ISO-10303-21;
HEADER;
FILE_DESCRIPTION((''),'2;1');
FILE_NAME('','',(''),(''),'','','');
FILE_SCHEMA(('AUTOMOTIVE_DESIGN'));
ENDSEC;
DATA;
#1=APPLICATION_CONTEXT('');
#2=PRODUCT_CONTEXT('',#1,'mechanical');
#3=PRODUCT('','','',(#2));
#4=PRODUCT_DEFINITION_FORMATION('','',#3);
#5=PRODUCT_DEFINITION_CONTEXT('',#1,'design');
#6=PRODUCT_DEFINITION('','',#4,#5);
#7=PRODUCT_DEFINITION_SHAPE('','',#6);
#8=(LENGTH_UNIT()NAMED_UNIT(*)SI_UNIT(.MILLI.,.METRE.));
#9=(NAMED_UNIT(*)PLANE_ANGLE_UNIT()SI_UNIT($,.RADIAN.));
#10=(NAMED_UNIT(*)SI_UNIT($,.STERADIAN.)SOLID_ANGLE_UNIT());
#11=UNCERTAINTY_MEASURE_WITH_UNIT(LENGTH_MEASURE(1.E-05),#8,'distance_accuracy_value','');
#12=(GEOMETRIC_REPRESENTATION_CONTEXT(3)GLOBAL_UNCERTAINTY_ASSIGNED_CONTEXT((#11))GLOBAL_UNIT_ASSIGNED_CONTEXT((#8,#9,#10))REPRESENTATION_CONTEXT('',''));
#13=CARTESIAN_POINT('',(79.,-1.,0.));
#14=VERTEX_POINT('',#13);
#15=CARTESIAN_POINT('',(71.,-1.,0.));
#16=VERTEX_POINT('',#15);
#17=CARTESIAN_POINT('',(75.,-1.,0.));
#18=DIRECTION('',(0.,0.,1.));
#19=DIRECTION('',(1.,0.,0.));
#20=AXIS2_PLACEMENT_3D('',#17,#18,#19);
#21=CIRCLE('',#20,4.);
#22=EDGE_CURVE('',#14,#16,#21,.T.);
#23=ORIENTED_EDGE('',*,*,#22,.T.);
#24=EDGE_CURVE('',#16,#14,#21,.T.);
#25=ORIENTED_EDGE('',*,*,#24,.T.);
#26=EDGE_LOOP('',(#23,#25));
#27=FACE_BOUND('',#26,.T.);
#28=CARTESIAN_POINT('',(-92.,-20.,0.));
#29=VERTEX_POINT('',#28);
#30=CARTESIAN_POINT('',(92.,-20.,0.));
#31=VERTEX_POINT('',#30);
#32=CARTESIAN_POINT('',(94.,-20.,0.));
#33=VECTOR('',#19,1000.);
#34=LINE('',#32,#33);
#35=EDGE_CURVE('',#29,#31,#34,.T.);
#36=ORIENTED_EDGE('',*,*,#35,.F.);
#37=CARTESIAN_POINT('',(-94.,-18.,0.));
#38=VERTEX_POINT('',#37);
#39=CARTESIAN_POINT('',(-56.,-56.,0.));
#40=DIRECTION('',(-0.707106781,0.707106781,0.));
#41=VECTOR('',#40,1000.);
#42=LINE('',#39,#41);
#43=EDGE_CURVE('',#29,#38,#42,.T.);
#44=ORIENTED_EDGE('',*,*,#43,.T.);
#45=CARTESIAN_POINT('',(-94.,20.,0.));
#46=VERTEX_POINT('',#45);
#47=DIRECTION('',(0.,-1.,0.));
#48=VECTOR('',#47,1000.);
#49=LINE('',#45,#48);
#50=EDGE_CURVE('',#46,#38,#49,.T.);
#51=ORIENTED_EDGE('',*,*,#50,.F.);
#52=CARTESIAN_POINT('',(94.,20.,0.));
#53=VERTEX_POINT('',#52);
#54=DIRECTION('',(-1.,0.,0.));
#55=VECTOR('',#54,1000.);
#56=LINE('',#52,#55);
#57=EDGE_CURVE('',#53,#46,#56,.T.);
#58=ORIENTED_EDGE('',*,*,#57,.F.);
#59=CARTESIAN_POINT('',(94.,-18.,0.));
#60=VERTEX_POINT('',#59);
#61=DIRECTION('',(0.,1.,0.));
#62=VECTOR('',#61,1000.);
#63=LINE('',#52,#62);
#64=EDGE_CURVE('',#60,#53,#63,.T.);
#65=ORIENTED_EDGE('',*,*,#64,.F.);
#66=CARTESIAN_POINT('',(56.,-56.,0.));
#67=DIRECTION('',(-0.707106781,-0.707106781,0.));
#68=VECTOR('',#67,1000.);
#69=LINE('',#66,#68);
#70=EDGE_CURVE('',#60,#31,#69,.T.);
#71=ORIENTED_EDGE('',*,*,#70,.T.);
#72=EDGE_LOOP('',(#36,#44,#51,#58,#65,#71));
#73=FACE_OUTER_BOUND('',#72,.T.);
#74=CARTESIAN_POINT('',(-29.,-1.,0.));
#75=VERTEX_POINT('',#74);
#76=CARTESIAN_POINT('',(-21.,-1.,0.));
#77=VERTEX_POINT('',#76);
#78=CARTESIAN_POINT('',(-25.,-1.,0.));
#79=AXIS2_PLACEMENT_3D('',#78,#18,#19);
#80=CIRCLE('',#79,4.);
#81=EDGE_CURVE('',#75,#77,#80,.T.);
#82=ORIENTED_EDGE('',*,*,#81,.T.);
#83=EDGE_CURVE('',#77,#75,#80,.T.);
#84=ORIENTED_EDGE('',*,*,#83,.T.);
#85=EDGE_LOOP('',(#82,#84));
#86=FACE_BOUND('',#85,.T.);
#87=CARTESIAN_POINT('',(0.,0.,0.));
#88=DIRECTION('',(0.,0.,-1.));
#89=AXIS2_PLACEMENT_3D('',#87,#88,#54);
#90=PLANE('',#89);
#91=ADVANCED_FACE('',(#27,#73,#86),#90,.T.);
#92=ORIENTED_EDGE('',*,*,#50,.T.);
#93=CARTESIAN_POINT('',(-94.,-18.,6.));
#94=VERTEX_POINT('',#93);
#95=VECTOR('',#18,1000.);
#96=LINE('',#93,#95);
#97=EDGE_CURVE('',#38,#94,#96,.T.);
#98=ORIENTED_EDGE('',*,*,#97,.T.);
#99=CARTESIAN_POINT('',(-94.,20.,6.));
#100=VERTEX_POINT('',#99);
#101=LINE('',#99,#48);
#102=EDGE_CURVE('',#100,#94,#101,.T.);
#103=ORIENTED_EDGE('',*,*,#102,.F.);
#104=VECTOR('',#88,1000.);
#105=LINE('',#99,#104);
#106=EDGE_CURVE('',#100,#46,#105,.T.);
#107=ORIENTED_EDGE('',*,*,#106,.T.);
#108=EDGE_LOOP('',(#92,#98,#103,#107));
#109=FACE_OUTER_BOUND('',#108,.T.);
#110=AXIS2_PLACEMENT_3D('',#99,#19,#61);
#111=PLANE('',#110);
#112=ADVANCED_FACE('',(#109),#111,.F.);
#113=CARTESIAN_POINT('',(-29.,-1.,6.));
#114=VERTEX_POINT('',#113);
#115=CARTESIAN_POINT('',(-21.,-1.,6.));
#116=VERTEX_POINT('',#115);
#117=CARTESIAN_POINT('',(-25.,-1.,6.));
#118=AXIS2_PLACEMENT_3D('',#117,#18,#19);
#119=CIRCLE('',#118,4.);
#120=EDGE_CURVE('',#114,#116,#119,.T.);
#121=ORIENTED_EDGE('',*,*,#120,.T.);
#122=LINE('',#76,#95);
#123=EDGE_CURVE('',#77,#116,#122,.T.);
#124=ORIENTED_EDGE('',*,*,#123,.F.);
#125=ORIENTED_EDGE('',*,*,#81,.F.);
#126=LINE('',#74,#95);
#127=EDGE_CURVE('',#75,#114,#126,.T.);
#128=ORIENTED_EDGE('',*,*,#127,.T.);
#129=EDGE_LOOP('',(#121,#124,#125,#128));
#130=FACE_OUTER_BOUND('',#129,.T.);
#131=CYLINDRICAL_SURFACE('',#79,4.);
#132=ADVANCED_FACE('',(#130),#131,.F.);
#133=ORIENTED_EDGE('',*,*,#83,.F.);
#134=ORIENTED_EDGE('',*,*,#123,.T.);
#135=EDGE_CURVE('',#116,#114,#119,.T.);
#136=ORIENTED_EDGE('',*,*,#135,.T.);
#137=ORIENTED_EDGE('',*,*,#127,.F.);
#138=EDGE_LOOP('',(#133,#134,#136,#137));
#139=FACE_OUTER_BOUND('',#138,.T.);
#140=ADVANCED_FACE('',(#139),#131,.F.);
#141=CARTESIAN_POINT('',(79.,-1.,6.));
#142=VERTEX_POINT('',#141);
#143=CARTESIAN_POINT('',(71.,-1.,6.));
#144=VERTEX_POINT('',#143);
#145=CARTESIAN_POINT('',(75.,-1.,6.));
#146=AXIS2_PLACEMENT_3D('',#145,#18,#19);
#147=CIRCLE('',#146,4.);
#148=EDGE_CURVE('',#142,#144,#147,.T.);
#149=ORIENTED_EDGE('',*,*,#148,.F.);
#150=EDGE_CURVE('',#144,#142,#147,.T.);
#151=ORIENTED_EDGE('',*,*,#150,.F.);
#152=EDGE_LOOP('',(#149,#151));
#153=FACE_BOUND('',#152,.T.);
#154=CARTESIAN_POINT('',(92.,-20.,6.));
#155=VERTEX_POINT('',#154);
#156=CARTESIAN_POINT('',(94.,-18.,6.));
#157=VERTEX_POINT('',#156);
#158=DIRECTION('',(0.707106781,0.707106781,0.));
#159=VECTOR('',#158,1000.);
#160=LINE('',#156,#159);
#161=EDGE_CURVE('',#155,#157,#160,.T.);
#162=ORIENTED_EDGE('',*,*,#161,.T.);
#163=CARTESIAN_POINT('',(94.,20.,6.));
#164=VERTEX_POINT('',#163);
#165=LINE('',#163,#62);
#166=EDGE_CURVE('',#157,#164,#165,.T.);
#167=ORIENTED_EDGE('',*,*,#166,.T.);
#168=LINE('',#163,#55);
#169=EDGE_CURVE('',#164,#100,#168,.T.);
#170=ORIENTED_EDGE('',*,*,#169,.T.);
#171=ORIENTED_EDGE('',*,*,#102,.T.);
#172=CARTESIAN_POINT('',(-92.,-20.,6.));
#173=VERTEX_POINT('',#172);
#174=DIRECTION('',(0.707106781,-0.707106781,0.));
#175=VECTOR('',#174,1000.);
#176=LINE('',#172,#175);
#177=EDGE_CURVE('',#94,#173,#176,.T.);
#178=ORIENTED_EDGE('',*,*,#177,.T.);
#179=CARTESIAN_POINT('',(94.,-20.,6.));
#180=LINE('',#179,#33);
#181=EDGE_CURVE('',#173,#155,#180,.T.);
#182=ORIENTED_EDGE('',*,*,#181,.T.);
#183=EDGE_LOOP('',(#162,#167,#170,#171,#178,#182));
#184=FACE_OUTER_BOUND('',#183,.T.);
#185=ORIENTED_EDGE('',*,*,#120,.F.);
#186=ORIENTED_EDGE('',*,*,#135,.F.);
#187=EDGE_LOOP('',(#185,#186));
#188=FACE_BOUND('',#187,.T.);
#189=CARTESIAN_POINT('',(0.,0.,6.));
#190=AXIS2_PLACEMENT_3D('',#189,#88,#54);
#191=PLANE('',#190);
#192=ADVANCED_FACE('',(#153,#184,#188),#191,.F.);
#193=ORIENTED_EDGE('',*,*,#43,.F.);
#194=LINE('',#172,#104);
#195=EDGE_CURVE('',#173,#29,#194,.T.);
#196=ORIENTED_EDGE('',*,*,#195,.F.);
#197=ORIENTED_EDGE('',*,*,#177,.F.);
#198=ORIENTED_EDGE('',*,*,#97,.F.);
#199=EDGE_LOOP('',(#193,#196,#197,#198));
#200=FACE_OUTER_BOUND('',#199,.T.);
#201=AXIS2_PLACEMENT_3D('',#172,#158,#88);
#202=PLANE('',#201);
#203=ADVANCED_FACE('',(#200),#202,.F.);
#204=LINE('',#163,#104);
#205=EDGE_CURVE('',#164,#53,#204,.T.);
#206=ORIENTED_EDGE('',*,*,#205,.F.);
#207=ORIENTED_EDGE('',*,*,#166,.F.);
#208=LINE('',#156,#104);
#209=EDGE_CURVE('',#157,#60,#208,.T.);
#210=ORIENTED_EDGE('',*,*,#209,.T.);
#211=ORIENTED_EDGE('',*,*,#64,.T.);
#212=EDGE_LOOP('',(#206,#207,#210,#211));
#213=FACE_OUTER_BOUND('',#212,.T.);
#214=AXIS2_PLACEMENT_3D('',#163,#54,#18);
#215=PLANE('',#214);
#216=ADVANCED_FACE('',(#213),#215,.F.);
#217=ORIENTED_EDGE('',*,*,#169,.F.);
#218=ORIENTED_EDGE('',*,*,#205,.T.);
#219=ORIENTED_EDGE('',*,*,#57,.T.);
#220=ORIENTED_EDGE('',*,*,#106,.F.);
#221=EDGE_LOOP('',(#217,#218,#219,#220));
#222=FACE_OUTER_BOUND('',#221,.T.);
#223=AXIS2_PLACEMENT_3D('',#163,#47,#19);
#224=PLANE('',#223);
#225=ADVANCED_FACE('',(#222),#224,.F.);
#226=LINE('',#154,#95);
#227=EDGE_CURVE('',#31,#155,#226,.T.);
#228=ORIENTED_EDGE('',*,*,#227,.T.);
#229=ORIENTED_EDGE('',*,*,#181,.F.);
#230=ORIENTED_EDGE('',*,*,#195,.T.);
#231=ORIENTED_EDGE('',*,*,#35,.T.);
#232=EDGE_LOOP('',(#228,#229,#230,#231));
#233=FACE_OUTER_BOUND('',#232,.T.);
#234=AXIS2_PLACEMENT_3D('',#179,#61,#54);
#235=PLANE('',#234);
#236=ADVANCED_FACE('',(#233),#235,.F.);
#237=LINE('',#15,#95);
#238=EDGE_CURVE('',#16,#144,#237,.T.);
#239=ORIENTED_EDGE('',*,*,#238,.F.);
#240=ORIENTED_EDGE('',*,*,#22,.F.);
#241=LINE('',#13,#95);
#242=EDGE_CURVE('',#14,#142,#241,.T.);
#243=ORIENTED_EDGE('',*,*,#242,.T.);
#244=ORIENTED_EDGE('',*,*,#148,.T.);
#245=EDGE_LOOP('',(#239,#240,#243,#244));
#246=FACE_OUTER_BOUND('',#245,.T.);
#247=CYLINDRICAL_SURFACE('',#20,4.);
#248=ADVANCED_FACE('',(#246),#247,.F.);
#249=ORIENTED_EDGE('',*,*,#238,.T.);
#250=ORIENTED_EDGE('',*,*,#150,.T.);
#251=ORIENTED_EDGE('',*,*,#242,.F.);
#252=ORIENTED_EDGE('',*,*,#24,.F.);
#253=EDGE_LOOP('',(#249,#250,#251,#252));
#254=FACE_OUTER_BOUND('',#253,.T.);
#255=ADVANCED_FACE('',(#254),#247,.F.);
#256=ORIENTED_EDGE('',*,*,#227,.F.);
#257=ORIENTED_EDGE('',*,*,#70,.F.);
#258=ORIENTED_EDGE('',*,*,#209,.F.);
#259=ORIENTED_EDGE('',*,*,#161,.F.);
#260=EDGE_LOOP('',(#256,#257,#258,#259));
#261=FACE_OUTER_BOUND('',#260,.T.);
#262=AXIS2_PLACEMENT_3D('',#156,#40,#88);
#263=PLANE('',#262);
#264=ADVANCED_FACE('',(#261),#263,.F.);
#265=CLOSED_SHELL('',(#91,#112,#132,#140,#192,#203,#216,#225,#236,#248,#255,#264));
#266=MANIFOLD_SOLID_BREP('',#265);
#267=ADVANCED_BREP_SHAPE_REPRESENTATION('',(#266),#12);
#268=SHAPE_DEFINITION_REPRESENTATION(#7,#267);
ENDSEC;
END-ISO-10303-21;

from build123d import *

# Parameters (mm, degrees)
SKETCH1_W           = 188
SKETCH1_H           = 40
BOSS_EXTRUDE1_DEPTH = 6
SKETCH2_R           = 4
CUT_EXTRUDE1_DEPTH  = 6
CHAMFER1_SIZE       = 2


with BuildPart() as part:
    # Sketch1 → Boss-Extrude1 (new body)
    with BuildSketch(Plane.XY):
        Rectangle(SKETCH1_W, SKETCH1_H)
    extrude(amount=BOSS_EXTRUDE1_DEPTH)

    # Sketch2 → Cut-Extrude1 (cut)
    with BuildSketch(Plane.XY.offset(6)):
        with Locations((-25, -1)):
            Circle(SKETCH2_R)
        with Locations((75, -1)):
            Circle(SKETCH2_R)
    extrude(amount=-CUT_EXTRUDE1_DEPTH, mode=Mode.SUBTRACT)

    # Chamfer1
    chamfer1_edges = [part.edges().sort_by_distance(p)[0] for p in [
        (94, -20, 3),
        (-94, -20, 3),
    ]]
    chamfer(chamfer1_edges, length=CHAMFER1_SIZE)


solid = part.part
